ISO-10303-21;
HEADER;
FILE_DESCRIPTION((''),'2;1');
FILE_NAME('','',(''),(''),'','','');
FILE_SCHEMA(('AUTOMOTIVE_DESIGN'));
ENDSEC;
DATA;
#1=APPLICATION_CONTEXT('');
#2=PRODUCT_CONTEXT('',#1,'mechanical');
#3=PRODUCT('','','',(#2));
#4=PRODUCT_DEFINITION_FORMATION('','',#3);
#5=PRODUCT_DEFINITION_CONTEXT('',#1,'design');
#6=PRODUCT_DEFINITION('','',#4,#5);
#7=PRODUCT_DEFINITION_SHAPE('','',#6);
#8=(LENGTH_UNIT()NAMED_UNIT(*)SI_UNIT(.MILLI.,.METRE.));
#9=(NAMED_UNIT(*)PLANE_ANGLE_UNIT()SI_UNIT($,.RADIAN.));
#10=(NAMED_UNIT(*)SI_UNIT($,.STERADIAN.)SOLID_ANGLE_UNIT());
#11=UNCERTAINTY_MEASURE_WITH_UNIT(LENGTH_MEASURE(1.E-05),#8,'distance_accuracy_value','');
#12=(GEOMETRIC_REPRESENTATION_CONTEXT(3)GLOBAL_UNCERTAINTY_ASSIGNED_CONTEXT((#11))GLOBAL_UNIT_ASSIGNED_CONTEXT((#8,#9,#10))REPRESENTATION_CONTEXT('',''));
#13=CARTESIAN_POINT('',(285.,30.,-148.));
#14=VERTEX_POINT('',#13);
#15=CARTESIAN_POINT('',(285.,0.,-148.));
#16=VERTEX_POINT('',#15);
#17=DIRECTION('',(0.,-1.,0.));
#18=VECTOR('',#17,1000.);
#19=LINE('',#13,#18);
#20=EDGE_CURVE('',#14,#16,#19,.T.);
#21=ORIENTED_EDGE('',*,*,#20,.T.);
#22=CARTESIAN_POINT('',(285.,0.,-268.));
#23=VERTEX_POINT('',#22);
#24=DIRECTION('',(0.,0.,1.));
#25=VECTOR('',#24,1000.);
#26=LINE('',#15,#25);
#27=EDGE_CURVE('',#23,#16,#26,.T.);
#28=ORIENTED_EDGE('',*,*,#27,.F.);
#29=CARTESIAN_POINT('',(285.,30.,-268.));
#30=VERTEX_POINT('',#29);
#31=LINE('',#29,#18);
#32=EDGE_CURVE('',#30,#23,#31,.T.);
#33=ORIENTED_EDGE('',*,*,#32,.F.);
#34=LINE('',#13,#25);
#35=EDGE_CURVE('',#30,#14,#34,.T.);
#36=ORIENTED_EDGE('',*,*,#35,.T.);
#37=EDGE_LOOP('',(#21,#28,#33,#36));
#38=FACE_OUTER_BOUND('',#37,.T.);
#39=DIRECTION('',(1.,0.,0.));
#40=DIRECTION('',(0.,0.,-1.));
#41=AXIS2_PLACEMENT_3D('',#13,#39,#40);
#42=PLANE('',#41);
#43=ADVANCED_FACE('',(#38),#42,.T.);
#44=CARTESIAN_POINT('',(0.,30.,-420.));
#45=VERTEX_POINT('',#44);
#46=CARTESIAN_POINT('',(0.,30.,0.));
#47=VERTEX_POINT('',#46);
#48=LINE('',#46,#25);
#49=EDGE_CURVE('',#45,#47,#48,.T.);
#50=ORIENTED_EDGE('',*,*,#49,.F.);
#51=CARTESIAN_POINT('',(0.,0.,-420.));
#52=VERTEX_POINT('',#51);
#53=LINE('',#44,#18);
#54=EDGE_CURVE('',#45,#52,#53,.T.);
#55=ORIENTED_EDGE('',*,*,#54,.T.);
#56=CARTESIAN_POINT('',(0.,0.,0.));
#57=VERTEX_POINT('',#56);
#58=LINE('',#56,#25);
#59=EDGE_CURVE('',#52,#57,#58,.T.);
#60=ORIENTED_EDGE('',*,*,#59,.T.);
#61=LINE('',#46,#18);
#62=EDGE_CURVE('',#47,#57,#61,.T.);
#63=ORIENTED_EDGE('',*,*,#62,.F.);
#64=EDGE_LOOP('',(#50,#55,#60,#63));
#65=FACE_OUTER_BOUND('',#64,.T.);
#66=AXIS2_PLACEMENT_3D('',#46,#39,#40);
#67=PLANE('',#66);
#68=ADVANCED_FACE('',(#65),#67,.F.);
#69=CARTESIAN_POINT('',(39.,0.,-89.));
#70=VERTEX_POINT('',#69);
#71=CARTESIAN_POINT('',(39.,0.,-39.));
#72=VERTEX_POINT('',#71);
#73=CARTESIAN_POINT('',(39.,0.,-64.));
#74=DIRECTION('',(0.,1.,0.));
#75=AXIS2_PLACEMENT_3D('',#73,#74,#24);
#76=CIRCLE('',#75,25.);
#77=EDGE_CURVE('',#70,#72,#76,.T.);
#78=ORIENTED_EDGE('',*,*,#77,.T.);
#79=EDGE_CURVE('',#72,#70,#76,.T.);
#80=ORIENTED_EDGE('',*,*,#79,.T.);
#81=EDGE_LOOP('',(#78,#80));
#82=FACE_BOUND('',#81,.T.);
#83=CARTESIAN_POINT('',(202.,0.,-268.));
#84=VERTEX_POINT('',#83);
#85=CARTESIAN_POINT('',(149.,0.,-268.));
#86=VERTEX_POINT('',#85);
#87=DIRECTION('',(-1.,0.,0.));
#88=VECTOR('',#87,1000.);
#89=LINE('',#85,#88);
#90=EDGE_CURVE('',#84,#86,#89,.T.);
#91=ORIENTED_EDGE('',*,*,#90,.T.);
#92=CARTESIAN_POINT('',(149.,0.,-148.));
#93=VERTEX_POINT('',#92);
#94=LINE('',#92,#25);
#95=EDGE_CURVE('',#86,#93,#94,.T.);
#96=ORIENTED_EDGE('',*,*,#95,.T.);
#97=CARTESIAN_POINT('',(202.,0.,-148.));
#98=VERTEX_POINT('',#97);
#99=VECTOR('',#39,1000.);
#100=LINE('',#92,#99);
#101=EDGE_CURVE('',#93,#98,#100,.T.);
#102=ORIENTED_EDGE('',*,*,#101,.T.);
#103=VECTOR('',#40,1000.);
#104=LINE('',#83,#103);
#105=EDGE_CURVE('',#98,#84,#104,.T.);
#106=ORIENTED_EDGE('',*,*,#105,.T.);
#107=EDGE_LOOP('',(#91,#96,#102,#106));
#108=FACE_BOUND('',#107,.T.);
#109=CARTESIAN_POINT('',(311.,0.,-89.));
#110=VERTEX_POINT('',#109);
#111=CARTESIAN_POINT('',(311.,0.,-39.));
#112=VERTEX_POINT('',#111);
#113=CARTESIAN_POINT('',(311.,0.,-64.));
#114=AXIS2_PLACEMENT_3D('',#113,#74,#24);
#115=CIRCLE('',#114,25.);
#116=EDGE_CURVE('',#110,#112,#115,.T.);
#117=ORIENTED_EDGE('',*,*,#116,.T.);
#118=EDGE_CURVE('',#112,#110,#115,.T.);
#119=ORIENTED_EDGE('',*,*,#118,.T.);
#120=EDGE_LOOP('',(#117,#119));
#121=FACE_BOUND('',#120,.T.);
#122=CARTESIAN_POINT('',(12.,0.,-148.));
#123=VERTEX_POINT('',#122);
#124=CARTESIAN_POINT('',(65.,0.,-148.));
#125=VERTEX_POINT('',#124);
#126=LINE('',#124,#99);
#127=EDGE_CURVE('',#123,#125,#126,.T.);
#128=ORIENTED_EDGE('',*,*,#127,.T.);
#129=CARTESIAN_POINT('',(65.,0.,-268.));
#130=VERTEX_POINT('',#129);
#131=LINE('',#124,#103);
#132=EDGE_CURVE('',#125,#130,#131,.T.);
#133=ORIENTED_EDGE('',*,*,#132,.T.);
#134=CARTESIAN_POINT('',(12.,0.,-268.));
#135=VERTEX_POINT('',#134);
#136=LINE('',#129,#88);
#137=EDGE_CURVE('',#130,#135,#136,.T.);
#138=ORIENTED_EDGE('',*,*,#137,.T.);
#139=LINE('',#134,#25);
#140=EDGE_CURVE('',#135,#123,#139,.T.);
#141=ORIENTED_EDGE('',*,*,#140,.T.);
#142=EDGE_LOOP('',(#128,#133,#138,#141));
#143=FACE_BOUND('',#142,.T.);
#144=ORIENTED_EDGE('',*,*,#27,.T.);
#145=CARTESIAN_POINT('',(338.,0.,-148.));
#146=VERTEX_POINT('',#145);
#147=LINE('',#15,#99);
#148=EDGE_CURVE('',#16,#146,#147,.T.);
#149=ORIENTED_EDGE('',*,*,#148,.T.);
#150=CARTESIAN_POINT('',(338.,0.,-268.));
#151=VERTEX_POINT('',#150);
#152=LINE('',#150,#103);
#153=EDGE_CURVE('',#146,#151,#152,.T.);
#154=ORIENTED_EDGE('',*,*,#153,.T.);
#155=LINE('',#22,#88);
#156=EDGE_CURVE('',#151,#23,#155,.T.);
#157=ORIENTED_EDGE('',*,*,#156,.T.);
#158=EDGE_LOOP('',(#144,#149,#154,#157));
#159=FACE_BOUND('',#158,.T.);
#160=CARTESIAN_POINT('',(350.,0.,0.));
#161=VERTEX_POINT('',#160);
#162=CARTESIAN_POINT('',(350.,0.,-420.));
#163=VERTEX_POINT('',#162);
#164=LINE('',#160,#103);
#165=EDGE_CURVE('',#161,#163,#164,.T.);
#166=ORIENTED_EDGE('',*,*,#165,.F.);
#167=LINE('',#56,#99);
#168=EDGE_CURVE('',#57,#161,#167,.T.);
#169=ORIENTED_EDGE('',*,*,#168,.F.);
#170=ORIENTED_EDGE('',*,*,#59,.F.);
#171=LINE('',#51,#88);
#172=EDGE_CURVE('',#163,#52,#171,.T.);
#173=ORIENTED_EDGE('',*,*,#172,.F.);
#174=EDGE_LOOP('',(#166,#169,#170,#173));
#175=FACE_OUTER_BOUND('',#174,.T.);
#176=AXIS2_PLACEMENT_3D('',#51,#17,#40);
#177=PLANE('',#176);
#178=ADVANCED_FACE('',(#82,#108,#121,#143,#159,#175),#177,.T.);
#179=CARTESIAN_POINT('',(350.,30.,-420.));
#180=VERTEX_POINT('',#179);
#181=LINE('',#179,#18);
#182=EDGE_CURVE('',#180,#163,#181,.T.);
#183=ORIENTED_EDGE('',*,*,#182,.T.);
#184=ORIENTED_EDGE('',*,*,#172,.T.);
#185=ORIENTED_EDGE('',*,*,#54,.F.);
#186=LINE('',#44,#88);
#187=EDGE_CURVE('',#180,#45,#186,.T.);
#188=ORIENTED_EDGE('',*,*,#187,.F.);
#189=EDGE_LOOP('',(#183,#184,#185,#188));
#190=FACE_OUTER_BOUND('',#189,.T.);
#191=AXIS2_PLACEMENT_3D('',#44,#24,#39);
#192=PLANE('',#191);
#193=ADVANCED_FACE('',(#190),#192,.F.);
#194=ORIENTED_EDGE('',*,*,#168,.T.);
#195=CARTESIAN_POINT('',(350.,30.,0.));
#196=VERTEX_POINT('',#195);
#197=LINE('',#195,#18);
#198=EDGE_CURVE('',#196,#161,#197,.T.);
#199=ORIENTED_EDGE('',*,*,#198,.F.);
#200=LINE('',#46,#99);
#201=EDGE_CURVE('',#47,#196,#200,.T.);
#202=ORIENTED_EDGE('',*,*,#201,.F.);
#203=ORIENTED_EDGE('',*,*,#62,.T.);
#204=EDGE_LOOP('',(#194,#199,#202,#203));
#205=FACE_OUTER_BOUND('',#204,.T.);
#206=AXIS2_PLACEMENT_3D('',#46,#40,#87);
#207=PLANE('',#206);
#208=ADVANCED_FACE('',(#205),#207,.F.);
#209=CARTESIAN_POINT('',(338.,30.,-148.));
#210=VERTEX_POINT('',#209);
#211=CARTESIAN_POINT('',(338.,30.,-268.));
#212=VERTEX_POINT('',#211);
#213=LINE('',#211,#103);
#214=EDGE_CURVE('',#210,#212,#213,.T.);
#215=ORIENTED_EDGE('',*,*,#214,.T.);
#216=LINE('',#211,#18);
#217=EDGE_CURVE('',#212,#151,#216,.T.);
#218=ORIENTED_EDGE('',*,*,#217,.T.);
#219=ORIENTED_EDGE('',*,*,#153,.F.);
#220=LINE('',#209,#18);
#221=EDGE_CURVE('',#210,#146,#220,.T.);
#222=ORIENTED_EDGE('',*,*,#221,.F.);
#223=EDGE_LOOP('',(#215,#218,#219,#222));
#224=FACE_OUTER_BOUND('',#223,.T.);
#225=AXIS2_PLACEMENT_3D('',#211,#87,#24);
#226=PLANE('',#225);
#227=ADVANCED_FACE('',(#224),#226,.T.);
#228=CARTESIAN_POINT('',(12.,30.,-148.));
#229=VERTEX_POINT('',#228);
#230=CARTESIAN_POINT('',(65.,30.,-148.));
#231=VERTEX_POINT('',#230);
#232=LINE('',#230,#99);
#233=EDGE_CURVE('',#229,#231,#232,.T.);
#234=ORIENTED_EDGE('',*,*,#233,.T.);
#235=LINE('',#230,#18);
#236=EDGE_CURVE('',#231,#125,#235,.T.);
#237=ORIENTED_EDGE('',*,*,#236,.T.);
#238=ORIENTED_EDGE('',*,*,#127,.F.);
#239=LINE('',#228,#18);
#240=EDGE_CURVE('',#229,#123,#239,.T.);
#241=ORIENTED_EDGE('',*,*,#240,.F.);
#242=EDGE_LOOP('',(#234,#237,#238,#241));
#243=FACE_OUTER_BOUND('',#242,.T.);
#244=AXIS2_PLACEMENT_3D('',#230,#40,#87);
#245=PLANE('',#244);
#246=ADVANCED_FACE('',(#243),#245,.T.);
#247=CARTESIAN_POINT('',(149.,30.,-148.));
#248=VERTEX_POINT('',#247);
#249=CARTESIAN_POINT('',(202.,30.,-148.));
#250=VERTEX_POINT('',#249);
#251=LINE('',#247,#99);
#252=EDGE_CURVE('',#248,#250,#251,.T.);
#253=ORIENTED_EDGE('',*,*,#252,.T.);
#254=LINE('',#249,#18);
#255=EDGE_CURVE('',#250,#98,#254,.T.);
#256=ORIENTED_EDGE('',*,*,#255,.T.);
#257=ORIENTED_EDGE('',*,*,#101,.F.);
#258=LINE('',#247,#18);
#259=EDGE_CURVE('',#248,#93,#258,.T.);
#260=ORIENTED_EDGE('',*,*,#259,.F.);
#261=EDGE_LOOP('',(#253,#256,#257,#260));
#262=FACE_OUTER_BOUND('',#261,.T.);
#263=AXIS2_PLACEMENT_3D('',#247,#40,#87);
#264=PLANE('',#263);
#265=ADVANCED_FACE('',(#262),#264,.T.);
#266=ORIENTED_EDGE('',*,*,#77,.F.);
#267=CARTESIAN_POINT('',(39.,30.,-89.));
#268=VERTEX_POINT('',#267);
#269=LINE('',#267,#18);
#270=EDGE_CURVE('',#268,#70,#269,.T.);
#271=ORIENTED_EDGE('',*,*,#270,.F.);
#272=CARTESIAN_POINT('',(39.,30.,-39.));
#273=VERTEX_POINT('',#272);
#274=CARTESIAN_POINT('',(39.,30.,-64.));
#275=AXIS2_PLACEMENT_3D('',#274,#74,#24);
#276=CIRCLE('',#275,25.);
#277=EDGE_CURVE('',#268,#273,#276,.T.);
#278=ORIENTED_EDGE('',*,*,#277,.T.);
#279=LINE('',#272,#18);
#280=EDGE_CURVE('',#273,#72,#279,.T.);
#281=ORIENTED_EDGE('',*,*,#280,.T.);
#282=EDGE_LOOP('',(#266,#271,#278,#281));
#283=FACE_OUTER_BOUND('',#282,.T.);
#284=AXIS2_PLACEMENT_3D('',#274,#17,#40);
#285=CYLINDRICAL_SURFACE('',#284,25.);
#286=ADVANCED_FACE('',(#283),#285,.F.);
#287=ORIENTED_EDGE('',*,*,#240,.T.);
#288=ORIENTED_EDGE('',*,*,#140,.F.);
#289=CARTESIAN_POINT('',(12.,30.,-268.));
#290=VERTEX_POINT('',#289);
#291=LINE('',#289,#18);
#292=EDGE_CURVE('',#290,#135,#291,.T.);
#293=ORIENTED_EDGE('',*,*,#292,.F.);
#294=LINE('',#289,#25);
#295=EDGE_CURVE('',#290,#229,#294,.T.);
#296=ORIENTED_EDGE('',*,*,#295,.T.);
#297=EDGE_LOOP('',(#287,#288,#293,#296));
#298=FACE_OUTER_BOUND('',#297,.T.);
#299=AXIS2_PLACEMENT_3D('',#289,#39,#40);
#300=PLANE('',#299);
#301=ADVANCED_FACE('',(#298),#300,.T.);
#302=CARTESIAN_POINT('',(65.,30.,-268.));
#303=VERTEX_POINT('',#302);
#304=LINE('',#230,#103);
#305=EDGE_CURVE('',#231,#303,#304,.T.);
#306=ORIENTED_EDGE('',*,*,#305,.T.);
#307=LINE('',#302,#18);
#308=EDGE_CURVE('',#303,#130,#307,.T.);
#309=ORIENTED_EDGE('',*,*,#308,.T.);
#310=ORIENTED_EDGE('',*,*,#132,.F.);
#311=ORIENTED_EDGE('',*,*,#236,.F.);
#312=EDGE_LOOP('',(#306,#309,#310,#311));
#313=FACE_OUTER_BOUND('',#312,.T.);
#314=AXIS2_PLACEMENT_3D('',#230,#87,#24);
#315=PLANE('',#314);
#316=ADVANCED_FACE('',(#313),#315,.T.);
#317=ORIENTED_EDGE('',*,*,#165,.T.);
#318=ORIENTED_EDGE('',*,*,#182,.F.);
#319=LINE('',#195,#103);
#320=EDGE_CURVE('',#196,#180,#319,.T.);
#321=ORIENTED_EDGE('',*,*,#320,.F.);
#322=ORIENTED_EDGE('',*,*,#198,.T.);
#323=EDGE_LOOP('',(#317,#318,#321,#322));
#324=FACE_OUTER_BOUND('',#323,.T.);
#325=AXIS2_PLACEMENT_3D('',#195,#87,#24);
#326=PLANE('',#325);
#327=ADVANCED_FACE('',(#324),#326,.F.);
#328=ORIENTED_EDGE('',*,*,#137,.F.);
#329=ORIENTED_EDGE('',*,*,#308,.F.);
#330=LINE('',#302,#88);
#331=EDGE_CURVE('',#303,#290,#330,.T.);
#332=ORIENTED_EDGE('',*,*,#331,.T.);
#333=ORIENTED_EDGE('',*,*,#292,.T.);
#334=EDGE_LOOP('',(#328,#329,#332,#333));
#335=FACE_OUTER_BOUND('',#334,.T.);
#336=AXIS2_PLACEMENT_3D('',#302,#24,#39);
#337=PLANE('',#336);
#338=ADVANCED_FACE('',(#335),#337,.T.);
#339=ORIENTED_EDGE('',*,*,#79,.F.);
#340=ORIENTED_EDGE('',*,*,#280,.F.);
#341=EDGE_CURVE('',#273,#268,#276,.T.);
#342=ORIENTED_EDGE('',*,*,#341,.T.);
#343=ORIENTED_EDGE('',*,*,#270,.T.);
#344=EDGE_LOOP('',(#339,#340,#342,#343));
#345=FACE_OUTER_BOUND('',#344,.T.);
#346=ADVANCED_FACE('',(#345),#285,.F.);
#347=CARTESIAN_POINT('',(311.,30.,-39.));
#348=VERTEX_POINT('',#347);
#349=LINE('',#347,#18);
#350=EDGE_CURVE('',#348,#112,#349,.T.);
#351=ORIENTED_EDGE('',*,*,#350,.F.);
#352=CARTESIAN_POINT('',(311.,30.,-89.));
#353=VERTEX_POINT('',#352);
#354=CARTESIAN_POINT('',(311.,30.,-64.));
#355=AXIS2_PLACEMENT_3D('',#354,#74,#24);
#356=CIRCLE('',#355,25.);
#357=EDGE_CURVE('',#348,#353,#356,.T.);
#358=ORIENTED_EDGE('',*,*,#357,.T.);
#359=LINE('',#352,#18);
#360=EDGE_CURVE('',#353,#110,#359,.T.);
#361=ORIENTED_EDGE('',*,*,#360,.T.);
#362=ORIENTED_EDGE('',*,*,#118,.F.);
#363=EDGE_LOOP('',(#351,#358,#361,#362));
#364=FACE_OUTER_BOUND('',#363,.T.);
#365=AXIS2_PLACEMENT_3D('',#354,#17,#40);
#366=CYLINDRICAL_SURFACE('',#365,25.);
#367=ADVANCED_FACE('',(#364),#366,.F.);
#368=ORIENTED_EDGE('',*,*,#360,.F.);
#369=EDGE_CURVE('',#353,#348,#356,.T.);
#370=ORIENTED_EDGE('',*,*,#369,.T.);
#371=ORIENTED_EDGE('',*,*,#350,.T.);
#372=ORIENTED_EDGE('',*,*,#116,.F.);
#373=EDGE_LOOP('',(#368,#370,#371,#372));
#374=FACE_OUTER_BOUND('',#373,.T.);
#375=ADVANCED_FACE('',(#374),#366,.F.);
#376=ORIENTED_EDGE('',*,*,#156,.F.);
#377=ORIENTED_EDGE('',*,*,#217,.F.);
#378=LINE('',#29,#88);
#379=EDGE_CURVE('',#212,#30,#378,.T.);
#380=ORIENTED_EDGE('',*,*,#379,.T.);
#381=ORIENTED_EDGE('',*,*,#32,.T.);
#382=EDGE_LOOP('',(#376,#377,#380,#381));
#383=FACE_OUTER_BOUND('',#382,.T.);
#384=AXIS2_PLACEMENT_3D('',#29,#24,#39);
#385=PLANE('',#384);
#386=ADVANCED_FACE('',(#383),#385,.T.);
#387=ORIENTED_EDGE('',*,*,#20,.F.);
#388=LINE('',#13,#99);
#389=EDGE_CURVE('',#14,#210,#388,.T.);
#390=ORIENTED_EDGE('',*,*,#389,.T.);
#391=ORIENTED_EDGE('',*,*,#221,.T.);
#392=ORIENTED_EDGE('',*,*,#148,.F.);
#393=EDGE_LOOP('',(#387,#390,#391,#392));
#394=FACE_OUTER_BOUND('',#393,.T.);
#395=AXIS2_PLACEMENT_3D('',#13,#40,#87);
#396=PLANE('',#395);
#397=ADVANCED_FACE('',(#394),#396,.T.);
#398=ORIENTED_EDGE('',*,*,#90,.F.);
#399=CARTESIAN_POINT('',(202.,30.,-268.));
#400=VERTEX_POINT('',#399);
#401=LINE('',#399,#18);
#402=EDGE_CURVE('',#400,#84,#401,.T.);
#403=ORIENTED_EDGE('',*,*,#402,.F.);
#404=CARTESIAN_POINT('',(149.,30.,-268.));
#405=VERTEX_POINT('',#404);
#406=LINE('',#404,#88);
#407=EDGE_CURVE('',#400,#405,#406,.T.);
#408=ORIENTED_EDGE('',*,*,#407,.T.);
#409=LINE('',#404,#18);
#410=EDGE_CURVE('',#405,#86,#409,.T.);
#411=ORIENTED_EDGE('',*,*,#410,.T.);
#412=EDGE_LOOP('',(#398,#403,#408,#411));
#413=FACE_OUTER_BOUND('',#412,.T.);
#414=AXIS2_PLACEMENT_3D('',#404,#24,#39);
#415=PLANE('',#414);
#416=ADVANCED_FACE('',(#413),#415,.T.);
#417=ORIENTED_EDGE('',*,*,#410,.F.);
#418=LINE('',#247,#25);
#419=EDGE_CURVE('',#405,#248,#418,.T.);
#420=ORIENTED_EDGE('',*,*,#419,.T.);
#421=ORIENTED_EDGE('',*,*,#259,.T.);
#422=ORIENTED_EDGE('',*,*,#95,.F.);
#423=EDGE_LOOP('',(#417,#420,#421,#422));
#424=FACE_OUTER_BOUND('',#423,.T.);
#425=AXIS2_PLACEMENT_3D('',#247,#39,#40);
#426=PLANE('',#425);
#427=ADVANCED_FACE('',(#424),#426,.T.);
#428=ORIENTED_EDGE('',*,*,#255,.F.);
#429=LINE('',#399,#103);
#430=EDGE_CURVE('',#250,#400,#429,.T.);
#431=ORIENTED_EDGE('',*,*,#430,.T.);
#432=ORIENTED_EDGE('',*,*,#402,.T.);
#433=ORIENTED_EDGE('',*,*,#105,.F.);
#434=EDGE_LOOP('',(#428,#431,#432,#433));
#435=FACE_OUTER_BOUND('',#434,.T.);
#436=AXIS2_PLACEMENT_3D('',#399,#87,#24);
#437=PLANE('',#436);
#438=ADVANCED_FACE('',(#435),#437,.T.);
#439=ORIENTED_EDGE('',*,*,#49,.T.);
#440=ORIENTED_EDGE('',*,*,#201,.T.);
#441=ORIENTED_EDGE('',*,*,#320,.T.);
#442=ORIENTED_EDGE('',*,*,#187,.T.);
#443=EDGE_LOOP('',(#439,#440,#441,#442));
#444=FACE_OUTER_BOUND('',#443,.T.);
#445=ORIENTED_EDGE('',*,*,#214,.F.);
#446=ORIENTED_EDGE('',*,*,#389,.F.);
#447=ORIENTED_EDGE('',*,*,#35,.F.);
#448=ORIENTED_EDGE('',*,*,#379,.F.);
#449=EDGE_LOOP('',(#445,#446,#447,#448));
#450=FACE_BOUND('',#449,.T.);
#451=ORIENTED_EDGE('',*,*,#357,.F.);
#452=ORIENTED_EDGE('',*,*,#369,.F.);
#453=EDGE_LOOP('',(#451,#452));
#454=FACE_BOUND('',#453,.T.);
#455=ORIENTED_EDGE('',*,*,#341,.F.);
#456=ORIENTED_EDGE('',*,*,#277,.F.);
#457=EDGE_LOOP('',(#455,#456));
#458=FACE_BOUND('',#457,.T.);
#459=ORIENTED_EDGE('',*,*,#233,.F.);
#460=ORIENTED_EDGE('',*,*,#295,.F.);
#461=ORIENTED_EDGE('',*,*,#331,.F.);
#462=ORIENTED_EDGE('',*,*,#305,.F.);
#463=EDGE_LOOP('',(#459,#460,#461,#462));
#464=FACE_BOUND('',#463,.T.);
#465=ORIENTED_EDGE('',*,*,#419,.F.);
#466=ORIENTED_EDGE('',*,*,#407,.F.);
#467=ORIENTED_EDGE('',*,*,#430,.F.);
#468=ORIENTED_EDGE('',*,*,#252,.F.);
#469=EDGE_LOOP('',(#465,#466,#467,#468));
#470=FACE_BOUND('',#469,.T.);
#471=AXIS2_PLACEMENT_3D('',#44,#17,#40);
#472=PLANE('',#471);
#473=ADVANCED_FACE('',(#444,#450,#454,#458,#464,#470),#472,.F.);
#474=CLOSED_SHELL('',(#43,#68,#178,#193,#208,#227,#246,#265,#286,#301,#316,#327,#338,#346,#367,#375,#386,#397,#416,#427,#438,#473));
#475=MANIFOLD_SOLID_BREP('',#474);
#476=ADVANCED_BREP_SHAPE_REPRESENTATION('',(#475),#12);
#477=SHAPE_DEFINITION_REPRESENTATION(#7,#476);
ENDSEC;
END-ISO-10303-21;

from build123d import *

# Parameters (mm, degrees)
SKETCH1_W           = 350
SKETCH1_H           = 420
SKETCH1_R           = 25
SKETCH1_W_2         = 53
SKETCH1_H_2         = 120
BOSS_EXTRUDE1_DEPTH = 30


with BuildPart() as part:
    # Sketch1 → Boss-Extrude1 (new body)
    with BuildSketch(Plane(origin=(0, 0, 0), x_dir=(1, 0, 0), z_dir=(0, 1, 0))):
        with Locations((175, 210)):
            Rectangle(SKETCH1_W, SKETCH1_H)
        with Locations(Location((311, 64, 0), (0, 0, 270))):
            Circle(SKETCH1_R, mode=Mode.SUBTRACT)
        with Locations(Location((39, 64, 0), (0, 0, 270))):
            Circle(SKETCH1_R, mode=Mode.SUBTRACT)
        with Locations((175.5, 208)):
            Rectangle(SKETCH1_W_2, SKETCH1_H_2, mode=Mode.SUBTRACT)
        with Locations((311.5, 208)):
            Rectangle(SKETCH1_W_2, SKETCH1_H_2, mode=Mode.SUBTRACT)
        with Locations((38.5, 208)):
            Rectangle(SKETCH1_W_2, SKETCH1_H_2, mode=Mode.SUBTRACT)
    extrude(amount=BOSS_EXTRUDE1_DEPTH)


solid = part.part
